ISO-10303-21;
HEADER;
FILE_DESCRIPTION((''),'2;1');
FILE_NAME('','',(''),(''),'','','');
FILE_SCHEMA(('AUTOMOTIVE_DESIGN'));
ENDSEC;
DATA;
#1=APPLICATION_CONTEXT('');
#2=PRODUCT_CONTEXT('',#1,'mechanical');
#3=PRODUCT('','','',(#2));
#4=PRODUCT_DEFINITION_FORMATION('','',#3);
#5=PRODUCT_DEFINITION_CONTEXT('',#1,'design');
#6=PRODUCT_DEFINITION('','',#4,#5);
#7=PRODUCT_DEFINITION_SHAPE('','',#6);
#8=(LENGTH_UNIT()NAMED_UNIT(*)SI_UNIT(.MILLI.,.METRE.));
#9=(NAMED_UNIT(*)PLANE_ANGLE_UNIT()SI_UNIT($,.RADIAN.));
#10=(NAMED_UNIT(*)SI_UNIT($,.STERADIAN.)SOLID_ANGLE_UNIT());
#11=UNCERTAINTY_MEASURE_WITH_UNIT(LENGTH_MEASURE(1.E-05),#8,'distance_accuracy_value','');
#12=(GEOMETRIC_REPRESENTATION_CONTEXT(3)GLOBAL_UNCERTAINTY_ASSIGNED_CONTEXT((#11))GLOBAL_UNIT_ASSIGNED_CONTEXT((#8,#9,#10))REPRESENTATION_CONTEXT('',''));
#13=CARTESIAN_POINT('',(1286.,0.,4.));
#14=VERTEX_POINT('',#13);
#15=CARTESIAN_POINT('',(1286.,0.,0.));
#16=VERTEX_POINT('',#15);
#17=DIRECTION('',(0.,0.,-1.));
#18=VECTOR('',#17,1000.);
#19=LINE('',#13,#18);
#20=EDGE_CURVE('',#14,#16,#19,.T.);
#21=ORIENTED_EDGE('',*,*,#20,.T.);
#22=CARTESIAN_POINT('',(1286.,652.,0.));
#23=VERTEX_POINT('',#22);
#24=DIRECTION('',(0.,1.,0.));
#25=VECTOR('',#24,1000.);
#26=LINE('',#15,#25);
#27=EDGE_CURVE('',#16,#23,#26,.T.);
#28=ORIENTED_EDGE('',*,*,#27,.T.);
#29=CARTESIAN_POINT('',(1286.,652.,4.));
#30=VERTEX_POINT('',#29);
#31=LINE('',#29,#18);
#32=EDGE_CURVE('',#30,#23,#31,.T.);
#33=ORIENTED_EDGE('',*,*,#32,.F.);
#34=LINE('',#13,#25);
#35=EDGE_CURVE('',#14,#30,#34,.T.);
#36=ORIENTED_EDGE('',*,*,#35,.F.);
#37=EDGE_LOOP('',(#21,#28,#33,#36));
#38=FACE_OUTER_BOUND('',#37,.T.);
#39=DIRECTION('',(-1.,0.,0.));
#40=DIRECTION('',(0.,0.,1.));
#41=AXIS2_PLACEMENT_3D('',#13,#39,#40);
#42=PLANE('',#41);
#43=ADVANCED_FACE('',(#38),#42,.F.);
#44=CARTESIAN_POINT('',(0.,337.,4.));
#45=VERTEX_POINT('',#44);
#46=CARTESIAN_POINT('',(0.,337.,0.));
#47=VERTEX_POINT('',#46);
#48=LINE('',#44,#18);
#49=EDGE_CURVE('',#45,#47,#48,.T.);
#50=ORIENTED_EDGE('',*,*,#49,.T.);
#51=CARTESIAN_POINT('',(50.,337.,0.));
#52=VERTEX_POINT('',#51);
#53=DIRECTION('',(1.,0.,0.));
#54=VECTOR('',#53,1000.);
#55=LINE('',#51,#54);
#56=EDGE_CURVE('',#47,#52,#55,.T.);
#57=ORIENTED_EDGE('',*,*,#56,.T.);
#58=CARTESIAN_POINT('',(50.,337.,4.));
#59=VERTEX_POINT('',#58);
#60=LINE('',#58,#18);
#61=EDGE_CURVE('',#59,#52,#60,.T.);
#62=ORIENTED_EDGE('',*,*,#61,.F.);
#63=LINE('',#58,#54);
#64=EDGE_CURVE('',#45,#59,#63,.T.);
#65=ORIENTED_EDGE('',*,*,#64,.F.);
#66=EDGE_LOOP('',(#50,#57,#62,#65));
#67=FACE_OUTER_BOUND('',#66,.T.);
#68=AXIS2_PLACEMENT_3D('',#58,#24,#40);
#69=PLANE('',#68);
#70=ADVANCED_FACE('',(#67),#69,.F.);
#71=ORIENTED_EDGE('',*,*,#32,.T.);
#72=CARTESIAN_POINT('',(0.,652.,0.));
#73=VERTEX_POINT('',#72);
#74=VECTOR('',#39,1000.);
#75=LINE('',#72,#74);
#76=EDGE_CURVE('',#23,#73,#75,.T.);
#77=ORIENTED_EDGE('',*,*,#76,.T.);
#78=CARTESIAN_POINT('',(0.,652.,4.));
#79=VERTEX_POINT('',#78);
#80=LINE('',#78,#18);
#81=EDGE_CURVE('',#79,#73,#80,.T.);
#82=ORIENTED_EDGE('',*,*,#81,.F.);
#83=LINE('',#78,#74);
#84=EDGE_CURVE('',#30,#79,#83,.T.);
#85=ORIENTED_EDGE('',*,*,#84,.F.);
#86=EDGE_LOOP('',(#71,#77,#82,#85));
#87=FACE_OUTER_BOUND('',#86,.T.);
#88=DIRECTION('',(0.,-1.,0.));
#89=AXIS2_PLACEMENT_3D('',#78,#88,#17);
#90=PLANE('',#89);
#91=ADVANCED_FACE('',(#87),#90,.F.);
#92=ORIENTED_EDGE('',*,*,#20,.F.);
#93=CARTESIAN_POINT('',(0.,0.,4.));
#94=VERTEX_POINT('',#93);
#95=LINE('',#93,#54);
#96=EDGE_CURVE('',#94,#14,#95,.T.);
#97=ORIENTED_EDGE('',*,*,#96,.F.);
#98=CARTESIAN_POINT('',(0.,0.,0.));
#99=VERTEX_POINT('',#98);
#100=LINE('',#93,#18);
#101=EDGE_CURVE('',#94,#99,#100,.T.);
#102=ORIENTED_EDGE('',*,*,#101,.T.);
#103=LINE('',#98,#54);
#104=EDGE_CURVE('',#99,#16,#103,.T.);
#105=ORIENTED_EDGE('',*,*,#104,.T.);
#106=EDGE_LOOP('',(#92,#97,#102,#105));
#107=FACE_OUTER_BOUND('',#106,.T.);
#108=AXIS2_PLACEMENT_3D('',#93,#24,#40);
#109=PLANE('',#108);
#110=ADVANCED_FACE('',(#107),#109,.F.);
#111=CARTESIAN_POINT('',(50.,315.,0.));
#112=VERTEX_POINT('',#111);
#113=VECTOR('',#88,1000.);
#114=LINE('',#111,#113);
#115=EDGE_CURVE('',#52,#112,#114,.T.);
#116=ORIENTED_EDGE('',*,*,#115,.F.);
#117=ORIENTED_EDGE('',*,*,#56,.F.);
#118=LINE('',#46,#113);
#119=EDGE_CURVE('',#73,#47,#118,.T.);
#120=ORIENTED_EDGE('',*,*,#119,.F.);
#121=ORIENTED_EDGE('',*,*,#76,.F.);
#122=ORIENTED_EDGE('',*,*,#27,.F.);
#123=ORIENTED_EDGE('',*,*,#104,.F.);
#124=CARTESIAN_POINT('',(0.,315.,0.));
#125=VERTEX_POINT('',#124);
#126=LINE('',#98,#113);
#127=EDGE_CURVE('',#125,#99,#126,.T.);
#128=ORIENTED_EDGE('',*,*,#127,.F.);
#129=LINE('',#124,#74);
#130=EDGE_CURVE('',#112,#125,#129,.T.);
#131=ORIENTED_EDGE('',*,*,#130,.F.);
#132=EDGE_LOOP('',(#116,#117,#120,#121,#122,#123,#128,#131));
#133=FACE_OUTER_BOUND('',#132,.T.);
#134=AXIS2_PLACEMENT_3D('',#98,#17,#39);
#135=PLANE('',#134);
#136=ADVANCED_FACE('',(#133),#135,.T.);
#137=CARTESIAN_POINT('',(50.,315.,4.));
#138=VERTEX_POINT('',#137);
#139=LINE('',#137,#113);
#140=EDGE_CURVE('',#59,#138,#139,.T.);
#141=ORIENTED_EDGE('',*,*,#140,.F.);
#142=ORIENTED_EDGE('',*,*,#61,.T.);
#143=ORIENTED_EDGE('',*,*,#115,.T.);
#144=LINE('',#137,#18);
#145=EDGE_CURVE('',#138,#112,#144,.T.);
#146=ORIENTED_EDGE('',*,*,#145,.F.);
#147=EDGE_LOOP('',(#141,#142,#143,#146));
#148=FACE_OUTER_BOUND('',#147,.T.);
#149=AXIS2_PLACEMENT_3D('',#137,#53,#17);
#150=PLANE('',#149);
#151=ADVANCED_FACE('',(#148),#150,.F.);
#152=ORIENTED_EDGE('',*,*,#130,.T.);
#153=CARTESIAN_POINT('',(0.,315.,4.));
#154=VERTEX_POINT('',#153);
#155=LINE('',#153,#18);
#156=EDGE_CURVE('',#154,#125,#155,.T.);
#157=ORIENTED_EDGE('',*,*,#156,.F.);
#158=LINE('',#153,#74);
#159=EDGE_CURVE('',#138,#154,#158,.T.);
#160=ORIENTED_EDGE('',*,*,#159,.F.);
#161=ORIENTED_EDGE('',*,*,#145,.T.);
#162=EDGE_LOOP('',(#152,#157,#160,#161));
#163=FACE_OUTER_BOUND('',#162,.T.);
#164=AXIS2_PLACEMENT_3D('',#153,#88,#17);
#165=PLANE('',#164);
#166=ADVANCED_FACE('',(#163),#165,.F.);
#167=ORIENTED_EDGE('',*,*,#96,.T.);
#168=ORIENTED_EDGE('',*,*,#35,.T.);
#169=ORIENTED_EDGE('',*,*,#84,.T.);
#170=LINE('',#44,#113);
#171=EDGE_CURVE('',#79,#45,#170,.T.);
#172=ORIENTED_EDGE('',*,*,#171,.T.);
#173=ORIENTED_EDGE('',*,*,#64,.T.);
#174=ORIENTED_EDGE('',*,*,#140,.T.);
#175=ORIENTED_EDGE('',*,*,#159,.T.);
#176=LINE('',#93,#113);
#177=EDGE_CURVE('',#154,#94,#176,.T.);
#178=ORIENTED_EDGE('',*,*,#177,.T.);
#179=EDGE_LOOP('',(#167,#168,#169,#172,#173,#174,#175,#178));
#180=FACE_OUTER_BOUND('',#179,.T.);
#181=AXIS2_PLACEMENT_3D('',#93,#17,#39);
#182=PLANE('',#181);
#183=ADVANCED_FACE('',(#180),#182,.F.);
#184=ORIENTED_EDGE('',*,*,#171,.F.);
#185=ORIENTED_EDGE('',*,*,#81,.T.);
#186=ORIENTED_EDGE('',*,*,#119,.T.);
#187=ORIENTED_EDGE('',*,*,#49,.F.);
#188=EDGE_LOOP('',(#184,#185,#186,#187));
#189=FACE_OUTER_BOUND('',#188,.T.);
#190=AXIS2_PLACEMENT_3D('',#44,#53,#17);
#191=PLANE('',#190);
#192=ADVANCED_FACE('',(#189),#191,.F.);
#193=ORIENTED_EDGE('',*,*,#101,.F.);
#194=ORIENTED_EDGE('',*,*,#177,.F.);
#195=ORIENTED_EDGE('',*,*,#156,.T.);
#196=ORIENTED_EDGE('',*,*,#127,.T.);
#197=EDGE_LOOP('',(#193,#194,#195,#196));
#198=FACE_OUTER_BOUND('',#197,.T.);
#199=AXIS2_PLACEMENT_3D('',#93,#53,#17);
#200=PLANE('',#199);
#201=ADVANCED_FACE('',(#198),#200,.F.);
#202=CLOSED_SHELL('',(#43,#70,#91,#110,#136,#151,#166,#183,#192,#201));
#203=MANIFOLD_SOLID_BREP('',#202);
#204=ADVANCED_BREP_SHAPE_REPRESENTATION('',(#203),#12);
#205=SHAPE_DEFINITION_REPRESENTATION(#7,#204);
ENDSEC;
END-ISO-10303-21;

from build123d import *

# Parameters (mm, degrees)
BOSS_EXTRUDE1_DEPTH = 4


with BuildPart() as part:
    # Sketch1 → Boss-Extrude1 (new body)
    with BuildSketch(Plane.XY):
        Polygon((0, 315), (50, 315), (50, 337), (0, 337), (0, 652), (1286, 652), (1286, 0), (0, 0), align=None)
    extrude(amount=BOSS_EXTRUDE1_DEPTH)


solid = part.part
